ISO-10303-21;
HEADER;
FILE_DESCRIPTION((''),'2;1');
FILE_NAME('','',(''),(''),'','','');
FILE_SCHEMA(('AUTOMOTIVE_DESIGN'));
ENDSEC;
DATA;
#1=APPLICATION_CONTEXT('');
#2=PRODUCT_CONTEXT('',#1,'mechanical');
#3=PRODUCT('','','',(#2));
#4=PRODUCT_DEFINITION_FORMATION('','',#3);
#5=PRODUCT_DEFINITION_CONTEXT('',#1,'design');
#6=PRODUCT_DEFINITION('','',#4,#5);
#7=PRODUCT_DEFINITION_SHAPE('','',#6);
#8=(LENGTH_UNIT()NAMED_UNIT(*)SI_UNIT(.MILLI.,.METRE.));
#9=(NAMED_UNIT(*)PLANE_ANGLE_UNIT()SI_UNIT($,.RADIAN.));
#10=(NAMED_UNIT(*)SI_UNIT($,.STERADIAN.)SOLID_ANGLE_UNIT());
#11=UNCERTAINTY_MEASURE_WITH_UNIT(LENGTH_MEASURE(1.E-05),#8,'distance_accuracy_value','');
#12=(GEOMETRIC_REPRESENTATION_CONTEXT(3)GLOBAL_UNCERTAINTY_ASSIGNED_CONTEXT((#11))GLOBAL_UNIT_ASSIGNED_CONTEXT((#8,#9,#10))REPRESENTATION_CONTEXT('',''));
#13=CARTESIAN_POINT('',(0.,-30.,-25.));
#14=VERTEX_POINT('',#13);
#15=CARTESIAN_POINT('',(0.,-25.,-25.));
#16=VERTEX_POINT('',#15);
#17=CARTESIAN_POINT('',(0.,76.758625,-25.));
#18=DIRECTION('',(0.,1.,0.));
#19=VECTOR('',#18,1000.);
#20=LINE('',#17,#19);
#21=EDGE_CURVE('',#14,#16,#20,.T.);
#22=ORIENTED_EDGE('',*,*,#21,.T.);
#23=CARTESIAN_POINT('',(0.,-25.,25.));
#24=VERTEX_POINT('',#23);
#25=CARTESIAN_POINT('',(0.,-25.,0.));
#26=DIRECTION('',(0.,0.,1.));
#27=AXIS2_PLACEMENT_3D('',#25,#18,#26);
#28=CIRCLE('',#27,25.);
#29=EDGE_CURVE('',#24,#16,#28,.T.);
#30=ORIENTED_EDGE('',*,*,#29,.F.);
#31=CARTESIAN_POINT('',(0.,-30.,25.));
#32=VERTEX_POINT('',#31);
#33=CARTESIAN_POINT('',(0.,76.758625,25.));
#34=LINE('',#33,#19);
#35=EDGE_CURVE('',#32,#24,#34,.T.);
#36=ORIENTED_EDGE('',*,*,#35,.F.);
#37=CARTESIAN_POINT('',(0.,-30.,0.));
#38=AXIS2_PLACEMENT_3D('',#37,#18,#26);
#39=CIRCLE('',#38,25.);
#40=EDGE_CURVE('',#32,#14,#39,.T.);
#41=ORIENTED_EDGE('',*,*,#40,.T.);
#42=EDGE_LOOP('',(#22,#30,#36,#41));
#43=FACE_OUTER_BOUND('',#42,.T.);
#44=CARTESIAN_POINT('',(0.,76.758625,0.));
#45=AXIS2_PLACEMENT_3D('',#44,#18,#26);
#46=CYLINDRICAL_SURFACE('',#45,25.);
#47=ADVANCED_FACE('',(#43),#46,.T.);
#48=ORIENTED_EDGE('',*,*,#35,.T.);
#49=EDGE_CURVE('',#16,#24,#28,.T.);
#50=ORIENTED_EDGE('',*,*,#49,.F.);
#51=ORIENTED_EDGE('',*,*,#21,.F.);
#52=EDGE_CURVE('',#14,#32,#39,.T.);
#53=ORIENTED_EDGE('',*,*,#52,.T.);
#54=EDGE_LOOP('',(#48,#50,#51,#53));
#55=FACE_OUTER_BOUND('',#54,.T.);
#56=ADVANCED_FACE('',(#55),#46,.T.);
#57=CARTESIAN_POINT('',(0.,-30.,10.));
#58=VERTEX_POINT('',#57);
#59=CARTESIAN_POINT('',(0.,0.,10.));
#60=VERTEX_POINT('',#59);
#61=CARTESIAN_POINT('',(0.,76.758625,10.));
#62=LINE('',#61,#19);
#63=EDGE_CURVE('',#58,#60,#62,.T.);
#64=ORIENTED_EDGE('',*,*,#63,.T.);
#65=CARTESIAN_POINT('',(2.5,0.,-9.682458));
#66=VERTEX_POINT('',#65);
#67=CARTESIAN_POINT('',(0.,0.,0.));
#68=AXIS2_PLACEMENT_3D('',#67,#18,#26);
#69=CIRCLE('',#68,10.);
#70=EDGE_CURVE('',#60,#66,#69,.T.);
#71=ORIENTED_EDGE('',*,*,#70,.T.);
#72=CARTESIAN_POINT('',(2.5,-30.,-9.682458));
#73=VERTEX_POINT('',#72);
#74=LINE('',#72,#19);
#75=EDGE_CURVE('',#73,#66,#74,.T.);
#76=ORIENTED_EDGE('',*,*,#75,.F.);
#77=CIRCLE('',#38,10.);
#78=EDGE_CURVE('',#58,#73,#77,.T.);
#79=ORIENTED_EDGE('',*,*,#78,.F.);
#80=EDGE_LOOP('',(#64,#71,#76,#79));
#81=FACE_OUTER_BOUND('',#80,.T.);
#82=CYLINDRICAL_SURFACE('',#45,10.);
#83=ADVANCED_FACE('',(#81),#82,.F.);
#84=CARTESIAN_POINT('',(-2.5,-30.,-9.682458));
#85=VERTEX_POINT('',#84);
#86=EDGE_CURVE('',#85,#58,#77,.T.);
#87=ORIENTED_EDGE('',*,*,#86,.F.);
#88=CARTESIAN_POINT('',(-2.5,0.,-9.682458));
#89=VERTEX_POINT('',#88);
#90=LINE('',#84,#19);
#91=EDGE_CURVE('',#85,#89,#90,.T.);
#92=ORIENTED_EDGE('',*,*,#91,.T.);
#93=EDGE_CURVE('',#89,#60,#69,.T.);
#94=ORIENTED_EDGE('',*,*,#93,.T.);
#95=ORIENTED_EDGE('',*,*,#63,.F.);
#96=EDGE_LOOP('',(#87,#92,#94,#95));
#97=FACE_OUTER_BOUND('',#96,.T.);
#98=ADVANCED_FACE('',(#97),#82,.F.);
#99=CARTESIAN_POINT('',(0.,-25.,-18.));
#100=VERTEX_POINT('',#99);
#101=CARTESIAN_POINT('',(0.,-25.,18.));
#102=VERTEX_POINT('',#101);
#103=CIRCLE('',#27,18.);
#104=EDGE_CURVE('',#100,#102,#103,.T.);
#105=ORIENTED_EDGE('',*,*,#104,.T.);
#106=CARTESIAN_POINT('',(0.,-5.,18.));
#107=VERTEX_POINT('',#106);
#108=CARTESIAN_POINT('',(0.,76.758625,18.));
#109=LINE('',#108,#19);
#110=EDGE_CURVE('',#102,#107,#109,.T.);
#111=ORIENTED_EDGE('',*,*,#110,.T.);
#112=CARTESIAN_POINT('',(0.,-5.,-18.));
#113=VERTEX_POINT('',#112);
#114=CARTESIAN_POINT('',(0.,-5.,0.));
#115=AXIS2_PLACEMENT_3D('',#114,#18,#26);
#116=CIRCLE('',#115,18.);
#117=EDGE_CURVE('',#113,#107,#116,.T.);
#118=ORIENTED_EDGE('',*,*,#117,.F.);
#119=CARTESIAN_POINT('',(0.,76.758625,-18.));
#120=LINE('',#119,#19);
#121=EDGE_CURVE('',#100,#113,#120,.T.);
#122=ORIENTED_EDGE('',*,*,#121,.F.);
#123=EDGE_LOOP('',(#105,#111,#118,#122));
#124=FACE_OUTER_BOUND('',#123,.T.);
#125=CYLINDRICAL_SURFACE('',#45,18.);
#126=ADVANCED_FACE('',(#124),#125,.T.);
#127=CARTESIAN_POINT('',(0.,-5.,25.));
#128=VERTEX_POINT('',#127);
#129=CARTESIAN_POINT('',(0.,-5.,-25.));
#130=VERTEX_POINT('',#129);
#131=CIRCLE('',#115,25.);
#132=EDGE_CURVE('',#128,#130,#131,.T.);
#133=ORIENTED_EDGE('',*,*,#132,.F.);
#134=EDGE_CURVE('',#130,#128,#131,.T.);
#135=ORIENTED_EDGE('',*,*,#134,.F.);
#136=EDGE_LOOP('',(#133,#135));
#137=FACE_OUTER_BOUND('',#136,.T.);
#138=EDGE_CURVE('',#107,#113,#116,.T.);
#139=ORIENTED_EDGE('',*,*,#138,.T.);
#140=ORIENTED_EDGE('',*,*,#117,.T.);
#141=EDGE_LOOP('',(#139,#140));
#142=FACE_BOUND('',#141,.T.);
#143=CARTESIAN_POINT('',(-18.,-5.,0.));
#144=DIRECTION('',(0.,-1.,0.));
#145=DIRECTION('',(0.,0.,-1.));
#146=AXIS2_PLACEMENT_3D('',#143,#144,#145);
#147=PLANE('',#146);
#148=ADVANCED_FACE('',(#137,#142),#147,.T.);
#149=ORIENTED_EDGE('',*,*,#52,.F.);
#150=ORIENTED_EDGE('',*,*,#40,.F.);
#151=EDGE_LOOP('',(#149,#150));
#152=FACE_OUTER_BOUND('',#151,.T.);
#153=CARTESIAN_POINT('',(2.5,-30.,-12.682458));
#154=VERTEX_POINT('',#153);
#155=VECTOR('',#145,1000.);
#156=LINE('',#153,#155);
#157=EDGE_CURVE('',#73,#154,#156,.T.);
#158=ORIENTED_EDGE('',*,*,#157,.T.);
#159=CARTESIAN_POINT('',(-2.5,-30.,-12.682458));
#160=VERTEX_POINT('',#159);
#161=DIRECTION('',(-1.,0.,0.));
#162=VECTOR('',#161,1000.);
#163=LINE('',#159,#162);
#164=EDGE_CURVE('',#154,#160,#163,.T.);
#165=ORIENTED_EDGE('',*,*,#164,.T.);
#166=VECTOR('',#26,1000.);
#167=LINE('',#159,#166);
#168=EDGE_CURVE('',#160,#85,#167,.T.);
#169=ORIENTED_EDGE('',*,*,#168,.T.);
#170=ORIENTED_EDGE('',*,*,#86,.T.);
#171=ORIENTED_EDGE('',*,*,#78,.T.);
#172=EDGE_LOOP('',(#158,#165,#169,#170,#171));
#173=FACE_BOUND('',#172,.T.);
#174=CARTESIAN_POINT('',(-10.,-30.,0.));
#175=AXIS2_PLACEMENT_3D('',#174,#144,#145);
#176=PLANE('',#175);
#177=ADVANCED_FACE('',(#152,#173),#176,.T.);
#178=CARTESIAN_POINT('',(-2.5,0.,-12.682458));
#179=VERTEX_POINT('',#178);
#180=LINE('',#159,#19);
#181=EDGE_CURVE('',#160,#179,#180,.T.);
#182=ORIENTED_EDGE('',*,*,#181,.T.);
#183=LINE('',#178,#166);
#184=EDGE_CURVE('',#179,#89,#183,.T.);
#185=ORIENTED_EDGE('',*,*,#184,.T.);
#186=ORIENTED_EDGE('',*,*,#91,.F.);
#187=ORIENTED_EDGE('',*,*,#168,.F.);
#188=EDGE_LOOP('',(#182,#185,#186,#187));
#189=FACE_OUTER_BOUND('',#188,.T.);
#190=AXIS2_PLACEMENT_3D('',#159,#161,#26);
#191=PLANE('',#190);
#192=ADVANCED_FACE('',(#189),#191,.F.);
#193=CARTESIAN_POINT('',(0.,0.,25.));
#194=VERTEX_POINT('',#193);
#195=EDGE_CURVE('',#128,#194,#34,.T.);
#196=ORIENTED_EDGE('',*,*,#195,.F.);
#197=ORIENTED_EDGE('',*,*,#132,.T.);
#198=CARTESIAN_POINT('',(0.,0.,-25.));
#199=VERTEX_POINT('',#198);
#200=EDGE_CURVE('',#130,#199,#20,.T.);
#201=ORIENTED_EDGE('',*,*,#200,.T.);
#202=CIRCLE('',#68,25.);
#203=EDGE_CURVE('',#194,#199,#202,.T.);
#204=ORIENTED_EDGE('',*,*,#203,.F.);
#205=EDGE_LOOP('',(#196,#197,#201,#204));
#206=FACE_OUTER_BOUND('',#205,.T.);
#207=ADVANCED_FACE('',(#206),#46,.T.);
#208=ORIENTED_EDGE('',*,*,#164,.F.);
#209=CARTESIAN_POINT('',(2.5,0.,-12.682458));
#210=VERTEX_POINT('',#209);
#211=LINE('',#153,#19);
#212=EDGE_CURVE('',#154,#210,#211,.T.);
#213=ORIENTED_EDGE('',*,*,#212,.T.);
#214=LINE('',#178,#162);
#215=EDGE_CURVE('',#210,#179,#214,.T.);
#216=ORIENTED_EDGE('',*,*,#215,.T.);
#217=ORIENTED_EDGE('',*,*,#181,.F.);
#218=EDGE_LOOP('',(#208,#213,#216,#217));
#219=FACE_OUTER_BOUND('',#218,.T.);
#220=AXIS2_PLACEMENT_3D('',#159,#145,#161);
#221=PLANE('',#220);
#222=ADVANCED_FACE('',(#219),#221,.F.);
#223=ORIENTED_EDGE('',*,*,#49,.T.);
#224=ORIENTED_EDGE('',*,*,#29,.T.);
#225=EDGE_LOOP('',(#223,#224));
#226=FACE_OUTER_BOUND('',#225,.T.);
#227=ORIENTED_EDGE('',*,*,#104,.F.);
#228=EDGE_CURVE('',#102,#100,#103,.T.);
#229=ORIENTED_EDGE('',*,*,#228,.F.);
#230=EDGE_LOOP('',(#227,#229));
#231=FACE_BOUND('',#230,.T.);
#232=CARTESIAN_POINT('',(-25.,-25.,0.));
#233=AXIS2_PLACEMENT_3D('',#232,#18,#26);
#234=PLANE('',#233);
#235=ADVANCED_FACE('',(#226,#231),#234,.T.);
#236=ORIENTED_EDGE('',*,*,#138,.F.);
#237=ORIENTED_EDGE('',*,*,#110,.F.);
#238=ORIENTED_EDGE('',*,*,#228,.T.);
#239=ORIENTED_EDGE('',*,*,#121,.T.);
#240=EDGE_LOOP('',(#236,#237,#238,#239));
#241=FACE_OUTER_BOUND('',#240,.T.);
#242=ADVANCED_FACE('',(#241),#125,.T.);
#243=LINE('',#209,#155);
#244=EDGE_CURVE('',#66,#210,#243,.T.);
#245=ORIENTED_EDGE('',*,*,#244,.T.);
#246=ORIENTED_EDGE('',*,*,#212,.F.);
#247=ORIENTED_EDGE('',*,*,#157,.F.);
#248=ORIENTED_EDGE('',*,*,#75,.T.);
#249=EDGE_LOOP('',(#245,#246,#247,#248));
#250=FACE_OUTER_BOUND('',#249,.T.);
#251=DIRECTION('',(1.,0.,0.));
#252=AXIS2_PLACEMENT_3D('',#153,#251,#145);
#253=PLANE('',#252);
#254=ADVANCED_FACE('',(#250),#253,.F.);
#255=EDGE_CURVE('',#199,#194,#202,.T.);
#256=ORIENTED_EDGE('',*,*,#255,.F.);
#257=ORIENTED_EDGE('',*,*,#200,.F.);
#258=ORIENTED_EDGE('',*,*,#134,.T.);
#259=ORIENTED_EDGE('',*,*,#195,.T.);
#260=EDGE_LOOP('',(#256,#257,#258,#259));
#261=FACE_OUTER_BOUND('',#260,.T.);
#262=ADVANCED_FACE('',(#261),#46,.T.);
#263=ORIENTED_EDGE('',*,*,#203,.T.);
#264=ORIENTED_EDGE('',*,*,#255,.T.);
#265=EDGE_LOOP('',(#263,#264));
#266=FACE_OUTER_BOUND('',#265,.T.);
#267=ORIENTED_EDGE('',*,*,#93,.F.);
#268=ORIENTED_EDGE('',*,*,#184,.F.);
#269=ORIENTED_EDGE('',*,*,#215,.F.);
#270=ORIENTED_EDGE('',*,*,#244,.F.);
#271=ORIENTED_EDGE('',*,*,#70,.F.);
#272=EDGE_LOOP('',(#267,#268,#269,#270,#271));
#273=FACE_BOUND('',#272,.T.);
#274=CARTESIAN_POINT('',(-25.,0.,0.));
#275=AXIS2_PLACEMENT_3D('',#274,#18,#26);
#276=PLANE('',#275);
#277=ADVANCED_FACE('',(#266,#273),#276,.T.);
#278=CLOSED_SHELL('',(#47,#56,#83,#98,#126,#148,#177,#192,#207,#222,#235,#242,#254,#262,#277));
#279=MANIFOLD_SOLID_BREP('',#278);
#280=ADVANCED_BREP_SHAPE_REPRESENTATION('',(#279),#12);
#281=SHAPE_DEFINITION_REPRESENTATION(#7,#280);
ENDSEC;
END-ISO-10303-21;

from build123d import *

# Parameters (mm, degrees)
CUT_EXTRUDE1_DEPTH = 47.368092477


with BuildPart() as part:
    # Sketch1 → Revolve1 (revolve)
    with BuildSketch(Plane.XY, mode=Mode.PRIVATE) as revolve1_sk:
        Polygon((-10, 0), (-10, -30), (-25, -30), (-25, -25), (-18, -25), (-18, -5), (-25, -5), (-25, 0), align=None)
    revolve(revolve1_sk.sketch.rotate(Axis((0, 76.758624558, 0), (0, -1, 0)), 270), axis=Axis((0, 76.758624558, 0), (0, -1, 0)))

    # Sketch2 → Cut-Extrude1 (cut, through all)
    with BuildSketch(Plane(origin=(0, 0, 0), x_dir=(1, 0, 0), z_dir=(0, 1, 0))):
        with BuildLine():
            Line((-2.5, 12.682458366), (-2.5, 9.682458366))
            ThreePointArc((-2.5, 9.682458366), (0, 10), (2.5, 9.682458366))
            Line((2.5, 9.682458366), (2.5, 12.682458366))
            Line((2.5, 12.682458366), (-2.5, 12.682458366))
        make_face()
    extrude(amount=-CUT_EXTRUDE1_DEPTH, mode=Mode.SUBTRACT)


solid = part.part
